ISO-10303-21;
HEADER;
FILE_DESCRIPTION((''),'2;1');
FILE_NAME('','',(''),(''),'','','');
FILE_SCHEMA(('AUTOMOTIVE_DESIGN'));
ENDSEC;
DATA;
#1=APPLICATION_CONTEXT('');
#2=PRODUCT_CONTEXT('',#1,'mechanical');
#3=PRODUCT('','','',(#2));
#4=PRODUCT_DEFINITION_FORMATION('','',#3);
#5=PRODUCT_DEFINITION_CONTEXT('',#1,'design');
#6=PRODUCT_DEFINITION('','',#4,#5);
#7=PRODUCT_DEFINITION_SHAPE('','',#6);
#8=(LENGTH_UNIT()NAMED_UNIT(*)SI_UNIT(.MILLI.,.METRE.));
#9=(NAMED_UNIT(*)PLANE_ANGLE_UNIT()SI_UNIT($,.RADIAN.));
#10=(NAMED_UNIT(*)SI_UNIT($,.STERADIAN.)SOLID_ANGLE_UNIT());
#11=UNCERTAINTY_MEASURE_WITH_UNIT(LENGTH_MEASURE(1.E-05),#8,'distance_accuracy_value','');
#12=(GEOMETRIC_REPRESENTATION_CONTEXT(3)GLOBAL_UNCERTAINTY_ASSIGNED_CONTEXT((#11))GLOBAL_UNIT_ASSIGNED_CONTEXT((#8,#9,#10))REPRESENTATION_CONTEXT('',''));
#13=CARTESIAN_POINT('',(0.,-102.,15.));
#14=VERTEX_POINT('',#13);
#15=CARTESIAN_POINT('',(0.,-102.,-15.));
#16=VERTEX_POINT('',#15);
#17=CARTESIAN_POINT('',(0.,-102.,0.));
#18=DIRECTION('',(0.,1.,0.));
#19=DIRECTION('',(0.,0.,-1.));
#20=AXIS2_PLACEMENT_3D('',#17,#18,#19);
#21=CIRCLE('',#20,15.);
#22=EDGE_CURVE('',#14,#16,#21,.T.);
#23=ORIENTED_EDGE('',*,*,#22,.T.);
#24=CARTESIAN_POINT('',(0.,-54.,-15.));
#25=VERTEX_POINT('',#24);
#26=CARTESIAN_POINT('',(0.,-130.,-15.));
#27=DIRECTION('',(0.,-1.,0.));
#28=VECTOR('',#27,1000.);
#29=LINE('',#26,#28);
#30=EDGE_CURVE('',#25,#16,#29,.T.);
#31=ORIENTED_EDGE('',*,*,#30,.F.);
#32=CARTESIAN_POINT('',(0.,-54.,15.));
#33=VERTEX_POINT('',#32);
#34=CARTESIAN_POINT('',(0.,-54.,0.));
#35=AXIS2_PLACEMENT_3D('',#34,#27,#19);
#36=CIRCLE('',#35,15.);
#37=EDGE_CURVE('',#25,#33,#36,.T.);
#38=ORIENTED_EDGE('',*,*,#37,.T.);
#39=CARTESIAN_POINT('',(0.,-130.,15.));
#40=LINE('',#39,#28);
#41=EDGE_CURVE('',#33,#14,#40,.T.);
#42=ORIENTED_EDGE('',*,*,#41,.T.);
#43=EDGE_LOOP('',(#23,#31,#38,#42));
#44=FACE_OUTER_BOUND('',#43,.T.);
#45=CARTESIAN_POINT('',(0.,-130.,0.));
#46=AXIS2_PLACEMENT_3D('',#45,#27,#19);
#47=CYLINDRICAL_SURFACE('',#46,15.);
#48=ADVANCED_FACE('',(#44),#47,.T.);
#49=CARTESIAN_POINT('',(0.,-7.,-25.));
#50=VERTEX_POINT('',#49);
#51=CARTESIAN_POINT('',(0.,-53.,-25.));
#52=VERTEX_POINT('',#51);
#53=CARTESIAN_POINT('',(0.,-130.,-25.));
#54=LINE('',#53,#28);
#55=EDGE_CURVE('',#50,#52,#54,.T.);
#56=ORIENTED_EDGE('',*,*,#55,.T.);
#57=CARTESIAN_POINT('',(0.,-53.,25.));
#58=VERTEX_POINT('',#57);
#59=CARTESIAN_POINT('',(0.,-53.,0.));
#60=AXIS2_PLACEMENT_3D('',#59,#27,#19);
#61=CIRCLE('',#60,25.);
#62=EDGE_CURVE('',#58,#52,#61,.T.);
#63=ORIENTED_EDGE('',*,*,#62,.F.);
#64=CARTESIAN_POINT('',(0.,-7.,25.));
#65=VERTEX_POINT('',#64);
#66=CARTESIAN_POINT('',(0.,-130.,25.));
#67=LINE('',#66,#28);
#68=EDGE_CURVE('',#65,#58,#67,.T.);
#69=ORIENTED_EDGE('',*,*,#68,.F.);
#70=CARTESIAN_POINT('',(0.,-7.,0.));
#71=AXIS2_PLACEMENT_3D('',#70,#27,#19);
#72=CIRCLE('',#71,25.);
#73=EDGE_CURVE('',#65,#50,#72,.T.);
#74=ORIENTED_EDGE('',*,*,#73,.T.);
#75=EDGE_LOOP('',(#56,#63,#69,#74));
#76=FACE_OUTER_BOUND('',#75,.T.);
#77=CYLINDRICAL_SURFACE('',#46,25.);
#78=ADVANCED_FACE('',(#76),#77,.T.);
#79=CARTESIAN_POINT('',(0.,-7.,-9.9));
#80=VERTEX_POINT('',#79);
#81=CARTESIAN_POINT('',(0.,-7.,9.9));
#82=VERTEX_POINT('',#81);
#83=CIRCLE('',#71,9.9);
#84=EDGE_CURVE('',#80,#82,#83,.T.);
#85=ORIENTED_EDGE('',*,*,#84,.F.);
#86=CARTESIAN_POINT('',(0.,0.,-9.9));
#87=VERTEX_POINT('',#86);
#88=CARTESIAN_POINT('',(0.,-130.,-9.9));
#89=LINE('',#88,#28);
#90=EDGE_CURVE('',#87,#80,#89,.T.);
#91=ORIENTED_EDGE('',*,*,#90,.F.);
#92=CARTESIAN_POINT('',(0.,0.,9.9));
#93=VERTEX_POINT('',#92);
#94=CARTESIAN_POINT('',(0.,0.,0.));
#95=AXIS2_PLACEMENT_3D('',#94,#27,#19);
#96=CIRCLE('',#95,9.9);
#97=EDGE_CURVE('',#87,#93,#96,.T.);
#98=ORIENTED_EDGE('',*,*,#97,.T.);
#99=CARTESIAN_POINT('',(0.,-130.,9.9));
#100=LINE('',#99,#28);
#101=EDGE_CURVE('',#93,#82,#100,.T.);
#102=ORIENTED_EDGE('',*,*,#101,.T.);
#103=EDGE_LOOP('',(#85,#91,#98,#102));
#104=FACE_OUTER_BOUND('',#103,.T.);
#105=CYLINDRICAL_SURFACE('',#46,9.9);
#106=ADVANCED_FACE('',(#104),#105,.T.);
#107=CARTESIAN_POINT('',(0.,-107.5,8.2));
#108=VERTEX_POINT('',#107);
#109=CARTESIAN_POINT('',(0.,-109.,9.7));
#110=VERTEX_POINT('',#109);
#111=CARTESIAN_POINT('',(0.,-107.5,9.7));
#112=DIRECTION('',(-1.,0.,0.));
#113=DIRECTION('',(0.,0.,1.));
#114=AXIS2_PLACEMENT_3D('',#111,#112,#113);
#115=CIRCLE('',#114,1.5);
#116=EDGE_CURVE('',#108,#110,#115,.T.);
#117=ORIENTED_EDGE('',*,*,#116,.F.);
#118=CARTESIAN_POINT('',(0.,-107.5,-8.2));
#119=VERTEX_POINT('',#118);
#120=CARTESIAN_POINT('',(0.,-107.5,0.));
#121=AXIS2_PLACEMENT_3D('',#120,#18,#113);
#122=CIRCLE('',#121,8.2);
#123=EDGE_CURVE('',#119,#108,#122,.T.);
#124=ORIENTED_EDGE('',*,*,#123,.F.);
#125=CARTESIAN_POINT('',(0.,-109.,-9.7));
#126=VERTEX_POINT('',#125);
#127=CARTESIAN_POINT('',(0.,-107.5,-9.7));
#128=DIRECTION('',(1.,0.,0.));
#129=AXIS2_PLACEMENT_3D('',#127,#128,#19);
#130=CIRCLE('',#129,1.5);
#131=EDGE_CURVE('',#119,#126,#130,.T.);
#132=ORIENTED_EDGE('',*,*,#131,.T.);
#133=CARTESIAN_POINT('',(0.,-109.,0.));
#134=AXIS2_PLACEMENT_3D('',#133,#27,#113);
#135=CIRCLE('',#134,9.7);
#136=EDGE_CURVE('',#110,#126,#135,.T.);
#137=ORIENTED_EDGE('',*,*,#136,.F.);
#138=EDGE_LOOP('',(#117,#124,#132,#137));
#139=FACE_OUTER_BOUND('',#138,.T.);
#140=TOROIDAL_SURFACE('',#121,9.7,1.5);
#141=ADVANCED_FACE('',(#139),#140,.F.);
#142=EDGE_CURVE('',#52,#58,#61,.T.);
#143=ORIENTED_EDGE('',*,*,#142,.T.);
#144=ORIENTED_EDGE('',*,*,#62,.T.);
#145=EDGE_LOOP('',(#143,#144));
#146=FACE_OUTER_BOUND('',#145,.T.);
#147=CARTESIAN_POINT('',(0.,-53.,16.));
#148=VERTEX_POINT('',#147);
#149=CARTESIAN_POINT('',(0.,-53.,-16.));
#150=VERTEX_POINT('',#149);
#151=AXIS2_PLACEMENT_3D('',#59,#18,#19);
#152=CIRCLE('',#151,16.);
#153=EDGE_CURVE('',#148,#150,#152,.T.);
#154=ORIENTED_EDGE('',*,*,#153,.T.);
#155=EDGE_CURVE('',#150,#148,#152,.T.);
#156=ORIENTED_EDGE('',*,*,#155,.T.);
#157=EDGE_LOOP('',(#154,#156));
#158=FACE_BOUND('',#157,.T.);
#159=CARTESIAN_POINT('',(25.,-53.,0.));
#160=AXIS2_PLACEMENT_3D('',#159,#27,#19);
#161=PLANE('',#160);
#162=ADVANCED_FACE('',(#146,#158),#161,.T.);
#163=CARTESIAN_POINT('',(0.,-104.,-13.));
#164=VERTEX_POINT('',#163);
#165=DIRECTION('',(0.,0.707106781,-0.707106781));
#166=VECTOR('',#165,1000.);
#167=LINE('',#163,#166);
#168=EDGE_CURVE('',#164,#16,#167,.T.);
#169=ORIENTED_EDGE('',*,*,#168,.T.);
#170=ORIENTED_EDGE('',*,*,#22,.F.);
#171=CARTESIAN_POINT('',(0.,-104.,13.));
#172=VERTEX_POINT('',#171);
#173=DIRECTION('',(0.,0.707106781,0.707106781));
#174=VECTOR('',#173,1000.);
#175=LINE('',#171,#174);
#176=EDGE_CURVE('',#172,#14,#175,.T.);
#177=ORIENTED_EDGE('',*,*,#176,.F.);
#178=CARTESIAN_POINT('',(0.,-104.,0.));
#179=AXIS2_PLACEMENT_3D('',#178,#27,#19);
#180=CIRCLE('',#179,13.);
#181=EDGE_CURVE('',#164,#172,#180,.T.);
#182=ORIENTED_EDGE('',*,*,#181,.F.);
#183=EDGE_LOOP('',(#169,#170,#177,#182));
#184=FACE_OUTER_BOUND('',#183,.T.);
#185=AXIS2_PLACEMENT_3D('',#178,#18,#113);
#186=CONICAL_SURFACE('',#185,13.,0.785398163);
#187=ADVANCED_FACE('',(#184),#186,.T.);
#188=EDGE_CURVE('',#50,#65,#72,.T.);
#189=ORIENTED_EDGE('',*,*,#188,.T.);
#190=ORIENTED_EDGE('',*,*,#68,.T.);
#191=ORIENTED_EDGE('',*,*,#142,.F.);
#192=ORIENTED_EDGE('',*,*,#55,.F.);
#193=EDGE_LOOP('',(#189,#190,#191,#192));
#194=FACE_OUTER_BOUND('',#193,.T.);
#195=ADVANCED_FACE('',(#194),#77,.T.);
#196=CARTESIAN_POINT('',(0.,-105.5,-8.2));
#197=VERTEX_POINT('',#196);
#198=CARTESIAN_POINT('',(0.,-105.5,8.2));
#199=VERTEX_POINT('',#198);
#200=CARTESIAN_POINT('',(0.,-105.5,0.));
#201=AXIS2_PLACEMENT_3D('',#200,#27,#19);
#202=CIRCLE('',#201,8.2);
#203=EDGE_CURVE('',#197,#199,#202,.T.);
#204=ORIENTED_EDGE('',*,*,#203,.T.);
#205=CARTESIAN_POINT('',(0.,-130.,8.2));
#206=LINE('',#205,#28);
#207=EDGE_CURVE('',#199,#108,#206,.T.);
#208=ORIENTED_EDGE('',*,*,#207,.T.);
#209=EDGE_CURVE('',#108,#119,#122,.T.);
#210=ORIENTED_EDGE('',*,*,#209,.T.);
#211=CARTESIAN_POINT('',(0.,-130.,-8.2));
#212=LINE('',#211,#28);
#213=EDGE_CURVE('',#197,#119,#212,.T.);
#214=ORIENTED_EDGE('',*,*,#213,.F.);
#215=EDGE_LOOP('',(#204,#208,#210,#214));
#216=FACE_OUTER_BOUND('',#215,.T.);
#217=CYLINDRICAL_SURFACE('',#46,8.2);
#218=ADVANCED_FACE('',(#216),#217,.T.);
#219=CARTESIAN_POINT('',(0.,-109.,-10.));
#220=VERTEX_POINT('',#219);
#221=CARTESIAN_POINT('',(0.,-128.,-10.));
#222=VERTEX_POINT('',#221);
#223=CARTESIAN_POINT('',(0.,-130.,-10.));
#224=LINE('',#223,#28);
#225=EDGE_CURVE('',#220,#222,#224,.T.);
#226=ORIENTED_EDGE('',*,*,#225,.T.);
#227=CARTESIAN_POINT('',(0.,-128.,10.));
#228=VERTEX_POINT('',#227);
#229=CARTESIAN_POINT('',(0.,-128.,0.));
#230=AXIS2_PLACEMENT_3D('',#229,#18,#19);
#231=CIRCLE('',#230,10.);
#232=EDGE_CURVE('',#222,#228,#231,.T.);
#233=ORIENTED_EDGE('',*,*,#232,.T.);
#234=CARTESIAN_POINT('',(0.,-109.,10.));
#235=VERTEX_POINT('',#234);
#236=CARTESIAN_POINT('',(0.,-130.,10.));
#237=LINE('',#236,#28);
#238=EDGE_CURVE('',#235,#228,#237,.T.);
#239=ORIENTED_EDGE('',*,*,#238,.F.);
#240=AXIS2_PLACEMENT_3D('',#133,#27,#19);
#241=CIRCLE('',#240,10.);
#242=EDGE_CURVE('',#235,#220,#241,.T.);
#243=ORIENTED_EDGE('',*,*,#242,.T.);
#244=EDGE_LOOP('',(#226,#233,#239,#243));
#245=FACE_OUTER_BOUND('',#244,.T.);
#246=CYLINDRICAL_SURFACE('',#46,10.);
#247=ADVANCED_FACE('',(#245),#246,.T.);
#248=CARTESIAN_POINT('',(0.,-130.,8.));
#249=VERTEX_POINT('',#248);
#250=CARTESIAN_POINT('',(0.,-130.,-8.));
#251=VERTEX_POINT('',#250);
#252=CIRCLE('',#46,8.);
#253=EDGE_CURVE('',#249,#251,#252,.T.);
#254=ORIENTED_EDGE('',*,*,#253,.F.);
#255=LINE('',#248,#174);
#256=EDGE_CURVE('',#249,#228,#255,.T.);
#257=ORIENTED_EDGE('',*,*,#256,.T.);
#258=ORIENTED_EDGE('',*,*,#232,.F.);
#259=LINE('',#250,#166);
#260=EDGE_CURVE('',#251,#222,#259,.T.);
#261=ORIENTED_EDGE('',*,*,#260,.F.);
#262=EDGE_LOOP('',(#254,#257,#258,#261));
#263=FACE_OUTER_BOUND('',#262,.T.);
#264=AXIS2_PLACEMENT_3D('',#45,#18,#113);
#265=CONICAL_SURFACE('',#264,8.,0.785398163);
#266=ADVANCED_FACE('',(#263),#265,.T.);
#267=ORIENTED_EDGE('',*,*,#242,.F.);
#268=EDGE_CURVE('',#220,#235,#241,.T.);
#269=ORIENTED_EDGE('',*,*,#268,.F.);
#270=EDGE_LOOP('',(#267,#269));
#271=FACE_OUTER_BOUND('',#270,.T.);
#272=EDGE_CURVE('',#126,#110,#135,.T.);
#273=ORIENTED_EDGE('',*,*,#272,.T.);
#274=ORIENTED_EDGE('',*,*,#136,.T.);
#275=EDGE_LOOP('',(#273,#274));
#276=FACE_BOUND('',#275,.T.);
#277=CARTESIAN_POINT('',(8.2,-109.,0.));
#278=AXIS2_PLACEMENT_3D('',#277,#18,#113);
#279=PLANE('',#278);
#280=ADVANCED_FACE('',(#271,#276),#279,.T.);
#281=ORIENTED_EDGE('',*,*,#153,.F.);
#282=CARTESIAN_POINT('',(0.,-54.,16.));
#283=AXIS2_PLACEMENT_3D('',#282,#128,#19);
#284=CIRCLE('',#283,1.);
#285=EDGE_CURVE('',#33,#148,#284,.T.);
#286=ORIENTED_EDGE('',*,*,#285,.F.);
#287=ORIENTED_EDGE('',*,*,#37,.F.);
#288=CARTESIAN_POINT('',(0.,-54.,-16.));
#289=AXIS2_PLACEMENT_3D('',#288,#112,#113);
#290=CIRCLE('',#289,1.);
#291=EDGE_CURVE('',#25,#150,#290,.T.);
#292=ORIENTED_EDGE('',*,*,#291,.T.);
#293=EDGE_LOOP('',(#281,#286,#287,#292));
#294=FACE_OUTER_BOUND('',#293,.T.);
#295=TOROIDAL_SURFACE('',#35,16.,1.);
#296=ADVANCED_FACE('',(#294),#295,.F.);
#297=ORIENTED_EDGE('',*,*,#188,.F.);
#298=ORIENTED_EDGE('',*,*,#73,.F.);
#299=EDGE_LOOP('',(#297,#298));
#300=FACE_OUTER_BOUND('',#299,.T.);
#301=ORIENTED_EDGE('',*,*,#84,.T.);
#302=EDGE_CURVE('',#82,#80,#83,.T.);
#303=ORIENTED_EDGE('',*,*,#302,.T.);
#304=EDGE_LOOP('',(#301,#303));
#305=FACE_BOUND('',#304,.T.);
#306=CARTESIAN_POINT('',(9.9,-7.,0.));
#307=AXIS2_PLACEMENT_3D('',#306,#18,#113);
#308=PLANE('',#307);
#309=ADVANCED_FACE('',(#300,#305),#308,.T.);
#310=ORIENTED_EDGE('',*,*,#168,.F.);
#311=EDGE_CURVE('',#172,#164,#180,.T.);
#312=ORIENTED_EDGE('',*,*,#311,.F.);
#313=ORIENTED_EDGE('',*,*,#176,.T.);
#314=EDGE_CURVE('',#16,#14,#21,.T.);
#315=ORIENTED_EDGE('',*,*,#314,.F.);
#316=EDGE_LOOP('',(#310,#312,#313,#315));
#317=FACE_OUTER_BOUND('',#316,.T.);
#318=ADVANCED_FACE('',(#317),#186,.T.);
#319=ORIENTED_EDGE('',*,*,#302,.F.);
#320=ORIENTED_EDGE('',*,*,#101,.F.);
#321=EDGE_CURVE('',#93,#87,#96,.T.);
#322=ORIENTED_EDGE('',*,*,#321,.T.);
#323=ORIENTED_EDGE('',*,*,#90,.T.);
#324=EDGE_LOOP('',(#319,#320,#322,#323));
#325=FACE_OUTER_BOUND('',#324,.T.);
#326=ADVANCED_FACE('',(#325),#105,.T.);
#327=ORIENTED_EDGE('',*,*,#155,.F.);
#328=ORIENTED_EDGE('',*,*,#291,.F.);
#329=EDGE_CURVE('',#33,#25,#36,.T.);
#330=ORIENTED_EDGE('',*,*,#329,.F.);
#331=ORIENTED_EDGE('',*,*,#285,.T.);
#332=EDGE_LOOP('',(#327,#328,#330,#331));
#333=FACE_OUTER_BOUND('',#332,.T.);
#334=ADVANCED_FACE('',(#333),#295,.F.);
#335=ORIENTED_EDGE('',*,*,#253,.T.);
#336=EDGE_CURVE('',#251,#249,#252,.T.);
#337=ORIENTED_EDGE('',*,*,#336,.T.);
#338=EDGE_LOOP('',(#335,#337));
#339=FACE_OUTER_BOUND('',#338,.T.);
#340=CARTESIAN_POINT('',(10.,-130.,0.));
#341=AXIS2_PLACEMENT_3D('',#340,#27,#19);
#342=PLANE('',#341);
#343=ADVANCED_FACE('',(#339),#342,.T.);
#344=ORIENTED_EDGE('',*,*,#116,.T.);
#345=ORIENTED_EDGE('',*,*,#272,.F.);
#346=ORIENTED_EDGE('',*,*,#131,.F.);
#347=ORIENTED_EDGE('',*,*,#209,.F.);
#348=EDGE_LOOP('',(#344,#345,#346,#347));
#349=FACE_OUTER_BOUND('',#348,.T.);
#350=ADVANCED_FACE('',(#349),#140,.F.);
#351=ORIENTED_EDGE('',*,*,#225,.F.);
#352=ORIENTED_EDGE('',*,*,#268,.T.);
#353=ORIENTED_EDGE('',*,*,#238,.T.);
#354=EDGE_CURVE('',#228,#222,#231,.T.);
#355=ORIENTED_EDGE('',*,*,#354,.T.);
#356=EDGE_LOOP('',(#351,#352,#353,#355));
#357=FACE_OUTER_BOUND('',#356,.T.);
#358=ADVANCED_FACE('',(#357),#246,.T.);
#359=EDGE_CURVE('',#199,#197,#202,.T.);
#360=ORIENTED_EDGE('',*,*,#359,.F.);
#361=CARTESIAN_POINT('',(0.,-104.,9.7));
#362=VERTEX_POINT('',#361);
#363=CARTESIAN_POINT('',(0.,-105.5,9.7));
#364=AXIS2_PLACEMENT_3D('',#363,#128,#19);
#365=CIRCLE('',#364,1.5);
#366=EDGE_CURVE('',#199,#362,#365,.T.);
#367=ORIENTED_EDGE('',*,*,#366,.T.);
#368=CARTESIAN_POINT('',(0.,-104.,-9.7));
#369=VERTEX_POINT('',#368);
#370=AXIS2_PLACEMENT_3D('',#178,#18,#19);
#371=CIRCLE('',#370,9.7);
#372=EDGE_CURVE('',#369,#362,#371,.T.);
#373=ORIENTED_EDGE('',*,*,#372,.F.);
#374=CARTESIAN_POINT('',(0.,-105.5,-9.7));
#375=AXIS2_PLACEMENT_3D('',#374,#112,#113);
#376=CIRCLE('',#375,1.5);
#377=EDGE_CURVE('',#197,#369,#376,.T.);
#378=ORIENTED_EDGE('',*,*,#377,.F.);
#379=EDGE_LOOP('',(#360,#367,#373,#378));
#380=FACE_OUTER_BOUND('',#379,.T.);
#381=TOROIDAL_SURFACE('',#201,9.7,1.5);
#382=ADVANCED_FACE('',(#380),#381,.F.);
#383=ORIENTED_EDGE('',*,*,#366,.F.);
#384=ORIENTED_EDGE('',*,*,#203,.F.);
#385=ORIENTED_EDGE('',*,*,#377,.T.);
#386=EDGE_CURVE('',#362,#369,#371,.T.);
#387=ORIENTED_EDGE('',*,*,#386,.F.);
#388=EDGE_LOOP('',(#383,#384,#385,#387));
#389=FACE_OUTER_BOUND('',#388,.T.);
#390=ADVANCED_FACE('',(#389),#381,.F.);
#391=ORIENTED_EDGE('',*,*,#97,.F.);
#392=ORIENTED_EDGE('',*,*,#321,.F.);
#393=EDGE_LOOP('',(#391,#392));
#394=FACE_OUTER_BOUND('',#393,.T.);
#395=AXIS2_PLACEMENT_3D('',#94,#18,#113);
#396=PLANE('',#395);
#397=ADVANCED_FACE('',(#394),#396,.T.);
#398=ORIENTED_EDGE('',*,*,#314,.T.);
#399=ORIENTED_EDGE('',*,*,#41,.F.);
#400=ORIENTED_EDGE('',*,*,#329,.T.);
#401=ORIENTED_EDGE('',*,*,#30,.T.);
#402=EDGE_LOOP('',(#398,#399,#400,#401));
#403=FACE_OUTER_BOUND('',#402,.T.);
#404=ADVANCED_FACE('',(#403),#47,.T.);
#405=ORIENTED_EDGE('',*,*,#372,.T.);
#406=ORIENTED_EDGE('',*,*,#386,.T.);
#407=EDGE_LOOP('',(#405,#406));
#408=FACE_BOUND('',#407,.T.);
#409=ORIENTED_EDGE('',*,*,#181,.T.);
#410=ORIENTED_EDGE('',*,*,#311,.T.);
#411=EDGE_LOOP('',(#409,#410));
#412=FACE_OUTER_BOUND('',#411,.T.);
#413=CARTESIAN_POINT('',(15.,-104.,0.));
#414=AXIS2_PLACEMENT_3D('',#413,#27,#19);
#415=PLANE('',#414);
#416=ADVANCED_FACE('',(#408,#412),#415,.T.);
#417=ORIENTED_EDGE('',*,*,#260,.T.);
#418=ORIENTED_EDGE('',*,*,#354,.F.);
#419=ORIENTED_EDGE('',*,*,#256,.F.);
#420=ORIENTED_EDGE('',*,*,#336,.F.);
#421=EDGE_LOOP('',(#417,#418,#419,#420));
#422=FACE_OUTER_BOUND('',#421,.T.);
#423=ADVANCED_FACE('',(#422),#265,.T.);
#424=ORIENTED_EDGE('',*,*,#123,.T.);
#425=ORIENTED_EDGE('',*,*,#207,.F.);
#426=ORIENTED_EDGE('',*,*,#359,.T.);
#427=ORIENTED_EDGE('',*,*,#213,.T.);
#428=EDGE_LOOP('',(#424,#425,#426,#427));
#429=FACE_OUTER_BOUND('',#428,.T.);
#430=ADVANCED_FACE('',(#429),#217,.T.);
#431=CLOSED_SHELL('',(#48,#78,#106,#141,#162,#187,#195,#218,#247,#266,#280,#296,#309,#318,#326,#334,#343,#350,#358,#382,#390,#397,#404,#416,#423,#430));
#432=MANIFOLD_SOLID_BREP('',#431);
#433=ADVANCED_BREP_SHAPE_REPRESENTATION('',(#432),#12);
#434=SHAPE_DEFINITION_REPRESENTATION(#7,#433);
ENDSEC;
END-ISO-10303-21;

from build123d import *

# Parameters (mm, degrees)
CHAMFER_1_SIZE = 2
FILLET_1_R     = 1
FILLET_2_R     = 1.5


with BuildPart() as part:
    # 草图1 → 旋转1 (revolve)
    with BuildSketch(Plane.XY, mode=Mode.PRIVATE) as revolve_1_sk:
        Polygon((0, 0), (9.9, 0), (9.9, -7), (25, -7), (25, -53), (15, -53), (15, -104), (8.2, -104), (8.2, -109), (10, -109), (10, -130), (0, -130), align=None)
    revolve(revolve_1_sk.sketch.rotate(Axis((0, -130, 0), (0, 1, 0)), 90), axis=Axis((0, -130, 0), (0, 1, 0)))

    # 倒角1
    chamfer_1_edges = [part.edges().sort_by_distance(p)[0] for p in [
        (0, -104, 15),
        (0, -130, 10),
    ]]
    chamfer(chamfer_1_edges, length=CHAMFER_1_SIZE)

    # 圆角1
    fillet_1_edges = [part.edges().sort_by_distance(p)[0] for p in [
        (0, -53, 15),
    ]]
    fillet(fillet_1_edges, radius=FILLET_1_R)

    # 圆角2
    fillet_2_edges = [part.edges().sort_by_distance(p)[0] for p in [
        (0, -109, 8.2),
        (0, -104, 8.2),
    ]]
    fillet(fillet_2_edges, radius=FILLET_2_R)


solid = part.part
